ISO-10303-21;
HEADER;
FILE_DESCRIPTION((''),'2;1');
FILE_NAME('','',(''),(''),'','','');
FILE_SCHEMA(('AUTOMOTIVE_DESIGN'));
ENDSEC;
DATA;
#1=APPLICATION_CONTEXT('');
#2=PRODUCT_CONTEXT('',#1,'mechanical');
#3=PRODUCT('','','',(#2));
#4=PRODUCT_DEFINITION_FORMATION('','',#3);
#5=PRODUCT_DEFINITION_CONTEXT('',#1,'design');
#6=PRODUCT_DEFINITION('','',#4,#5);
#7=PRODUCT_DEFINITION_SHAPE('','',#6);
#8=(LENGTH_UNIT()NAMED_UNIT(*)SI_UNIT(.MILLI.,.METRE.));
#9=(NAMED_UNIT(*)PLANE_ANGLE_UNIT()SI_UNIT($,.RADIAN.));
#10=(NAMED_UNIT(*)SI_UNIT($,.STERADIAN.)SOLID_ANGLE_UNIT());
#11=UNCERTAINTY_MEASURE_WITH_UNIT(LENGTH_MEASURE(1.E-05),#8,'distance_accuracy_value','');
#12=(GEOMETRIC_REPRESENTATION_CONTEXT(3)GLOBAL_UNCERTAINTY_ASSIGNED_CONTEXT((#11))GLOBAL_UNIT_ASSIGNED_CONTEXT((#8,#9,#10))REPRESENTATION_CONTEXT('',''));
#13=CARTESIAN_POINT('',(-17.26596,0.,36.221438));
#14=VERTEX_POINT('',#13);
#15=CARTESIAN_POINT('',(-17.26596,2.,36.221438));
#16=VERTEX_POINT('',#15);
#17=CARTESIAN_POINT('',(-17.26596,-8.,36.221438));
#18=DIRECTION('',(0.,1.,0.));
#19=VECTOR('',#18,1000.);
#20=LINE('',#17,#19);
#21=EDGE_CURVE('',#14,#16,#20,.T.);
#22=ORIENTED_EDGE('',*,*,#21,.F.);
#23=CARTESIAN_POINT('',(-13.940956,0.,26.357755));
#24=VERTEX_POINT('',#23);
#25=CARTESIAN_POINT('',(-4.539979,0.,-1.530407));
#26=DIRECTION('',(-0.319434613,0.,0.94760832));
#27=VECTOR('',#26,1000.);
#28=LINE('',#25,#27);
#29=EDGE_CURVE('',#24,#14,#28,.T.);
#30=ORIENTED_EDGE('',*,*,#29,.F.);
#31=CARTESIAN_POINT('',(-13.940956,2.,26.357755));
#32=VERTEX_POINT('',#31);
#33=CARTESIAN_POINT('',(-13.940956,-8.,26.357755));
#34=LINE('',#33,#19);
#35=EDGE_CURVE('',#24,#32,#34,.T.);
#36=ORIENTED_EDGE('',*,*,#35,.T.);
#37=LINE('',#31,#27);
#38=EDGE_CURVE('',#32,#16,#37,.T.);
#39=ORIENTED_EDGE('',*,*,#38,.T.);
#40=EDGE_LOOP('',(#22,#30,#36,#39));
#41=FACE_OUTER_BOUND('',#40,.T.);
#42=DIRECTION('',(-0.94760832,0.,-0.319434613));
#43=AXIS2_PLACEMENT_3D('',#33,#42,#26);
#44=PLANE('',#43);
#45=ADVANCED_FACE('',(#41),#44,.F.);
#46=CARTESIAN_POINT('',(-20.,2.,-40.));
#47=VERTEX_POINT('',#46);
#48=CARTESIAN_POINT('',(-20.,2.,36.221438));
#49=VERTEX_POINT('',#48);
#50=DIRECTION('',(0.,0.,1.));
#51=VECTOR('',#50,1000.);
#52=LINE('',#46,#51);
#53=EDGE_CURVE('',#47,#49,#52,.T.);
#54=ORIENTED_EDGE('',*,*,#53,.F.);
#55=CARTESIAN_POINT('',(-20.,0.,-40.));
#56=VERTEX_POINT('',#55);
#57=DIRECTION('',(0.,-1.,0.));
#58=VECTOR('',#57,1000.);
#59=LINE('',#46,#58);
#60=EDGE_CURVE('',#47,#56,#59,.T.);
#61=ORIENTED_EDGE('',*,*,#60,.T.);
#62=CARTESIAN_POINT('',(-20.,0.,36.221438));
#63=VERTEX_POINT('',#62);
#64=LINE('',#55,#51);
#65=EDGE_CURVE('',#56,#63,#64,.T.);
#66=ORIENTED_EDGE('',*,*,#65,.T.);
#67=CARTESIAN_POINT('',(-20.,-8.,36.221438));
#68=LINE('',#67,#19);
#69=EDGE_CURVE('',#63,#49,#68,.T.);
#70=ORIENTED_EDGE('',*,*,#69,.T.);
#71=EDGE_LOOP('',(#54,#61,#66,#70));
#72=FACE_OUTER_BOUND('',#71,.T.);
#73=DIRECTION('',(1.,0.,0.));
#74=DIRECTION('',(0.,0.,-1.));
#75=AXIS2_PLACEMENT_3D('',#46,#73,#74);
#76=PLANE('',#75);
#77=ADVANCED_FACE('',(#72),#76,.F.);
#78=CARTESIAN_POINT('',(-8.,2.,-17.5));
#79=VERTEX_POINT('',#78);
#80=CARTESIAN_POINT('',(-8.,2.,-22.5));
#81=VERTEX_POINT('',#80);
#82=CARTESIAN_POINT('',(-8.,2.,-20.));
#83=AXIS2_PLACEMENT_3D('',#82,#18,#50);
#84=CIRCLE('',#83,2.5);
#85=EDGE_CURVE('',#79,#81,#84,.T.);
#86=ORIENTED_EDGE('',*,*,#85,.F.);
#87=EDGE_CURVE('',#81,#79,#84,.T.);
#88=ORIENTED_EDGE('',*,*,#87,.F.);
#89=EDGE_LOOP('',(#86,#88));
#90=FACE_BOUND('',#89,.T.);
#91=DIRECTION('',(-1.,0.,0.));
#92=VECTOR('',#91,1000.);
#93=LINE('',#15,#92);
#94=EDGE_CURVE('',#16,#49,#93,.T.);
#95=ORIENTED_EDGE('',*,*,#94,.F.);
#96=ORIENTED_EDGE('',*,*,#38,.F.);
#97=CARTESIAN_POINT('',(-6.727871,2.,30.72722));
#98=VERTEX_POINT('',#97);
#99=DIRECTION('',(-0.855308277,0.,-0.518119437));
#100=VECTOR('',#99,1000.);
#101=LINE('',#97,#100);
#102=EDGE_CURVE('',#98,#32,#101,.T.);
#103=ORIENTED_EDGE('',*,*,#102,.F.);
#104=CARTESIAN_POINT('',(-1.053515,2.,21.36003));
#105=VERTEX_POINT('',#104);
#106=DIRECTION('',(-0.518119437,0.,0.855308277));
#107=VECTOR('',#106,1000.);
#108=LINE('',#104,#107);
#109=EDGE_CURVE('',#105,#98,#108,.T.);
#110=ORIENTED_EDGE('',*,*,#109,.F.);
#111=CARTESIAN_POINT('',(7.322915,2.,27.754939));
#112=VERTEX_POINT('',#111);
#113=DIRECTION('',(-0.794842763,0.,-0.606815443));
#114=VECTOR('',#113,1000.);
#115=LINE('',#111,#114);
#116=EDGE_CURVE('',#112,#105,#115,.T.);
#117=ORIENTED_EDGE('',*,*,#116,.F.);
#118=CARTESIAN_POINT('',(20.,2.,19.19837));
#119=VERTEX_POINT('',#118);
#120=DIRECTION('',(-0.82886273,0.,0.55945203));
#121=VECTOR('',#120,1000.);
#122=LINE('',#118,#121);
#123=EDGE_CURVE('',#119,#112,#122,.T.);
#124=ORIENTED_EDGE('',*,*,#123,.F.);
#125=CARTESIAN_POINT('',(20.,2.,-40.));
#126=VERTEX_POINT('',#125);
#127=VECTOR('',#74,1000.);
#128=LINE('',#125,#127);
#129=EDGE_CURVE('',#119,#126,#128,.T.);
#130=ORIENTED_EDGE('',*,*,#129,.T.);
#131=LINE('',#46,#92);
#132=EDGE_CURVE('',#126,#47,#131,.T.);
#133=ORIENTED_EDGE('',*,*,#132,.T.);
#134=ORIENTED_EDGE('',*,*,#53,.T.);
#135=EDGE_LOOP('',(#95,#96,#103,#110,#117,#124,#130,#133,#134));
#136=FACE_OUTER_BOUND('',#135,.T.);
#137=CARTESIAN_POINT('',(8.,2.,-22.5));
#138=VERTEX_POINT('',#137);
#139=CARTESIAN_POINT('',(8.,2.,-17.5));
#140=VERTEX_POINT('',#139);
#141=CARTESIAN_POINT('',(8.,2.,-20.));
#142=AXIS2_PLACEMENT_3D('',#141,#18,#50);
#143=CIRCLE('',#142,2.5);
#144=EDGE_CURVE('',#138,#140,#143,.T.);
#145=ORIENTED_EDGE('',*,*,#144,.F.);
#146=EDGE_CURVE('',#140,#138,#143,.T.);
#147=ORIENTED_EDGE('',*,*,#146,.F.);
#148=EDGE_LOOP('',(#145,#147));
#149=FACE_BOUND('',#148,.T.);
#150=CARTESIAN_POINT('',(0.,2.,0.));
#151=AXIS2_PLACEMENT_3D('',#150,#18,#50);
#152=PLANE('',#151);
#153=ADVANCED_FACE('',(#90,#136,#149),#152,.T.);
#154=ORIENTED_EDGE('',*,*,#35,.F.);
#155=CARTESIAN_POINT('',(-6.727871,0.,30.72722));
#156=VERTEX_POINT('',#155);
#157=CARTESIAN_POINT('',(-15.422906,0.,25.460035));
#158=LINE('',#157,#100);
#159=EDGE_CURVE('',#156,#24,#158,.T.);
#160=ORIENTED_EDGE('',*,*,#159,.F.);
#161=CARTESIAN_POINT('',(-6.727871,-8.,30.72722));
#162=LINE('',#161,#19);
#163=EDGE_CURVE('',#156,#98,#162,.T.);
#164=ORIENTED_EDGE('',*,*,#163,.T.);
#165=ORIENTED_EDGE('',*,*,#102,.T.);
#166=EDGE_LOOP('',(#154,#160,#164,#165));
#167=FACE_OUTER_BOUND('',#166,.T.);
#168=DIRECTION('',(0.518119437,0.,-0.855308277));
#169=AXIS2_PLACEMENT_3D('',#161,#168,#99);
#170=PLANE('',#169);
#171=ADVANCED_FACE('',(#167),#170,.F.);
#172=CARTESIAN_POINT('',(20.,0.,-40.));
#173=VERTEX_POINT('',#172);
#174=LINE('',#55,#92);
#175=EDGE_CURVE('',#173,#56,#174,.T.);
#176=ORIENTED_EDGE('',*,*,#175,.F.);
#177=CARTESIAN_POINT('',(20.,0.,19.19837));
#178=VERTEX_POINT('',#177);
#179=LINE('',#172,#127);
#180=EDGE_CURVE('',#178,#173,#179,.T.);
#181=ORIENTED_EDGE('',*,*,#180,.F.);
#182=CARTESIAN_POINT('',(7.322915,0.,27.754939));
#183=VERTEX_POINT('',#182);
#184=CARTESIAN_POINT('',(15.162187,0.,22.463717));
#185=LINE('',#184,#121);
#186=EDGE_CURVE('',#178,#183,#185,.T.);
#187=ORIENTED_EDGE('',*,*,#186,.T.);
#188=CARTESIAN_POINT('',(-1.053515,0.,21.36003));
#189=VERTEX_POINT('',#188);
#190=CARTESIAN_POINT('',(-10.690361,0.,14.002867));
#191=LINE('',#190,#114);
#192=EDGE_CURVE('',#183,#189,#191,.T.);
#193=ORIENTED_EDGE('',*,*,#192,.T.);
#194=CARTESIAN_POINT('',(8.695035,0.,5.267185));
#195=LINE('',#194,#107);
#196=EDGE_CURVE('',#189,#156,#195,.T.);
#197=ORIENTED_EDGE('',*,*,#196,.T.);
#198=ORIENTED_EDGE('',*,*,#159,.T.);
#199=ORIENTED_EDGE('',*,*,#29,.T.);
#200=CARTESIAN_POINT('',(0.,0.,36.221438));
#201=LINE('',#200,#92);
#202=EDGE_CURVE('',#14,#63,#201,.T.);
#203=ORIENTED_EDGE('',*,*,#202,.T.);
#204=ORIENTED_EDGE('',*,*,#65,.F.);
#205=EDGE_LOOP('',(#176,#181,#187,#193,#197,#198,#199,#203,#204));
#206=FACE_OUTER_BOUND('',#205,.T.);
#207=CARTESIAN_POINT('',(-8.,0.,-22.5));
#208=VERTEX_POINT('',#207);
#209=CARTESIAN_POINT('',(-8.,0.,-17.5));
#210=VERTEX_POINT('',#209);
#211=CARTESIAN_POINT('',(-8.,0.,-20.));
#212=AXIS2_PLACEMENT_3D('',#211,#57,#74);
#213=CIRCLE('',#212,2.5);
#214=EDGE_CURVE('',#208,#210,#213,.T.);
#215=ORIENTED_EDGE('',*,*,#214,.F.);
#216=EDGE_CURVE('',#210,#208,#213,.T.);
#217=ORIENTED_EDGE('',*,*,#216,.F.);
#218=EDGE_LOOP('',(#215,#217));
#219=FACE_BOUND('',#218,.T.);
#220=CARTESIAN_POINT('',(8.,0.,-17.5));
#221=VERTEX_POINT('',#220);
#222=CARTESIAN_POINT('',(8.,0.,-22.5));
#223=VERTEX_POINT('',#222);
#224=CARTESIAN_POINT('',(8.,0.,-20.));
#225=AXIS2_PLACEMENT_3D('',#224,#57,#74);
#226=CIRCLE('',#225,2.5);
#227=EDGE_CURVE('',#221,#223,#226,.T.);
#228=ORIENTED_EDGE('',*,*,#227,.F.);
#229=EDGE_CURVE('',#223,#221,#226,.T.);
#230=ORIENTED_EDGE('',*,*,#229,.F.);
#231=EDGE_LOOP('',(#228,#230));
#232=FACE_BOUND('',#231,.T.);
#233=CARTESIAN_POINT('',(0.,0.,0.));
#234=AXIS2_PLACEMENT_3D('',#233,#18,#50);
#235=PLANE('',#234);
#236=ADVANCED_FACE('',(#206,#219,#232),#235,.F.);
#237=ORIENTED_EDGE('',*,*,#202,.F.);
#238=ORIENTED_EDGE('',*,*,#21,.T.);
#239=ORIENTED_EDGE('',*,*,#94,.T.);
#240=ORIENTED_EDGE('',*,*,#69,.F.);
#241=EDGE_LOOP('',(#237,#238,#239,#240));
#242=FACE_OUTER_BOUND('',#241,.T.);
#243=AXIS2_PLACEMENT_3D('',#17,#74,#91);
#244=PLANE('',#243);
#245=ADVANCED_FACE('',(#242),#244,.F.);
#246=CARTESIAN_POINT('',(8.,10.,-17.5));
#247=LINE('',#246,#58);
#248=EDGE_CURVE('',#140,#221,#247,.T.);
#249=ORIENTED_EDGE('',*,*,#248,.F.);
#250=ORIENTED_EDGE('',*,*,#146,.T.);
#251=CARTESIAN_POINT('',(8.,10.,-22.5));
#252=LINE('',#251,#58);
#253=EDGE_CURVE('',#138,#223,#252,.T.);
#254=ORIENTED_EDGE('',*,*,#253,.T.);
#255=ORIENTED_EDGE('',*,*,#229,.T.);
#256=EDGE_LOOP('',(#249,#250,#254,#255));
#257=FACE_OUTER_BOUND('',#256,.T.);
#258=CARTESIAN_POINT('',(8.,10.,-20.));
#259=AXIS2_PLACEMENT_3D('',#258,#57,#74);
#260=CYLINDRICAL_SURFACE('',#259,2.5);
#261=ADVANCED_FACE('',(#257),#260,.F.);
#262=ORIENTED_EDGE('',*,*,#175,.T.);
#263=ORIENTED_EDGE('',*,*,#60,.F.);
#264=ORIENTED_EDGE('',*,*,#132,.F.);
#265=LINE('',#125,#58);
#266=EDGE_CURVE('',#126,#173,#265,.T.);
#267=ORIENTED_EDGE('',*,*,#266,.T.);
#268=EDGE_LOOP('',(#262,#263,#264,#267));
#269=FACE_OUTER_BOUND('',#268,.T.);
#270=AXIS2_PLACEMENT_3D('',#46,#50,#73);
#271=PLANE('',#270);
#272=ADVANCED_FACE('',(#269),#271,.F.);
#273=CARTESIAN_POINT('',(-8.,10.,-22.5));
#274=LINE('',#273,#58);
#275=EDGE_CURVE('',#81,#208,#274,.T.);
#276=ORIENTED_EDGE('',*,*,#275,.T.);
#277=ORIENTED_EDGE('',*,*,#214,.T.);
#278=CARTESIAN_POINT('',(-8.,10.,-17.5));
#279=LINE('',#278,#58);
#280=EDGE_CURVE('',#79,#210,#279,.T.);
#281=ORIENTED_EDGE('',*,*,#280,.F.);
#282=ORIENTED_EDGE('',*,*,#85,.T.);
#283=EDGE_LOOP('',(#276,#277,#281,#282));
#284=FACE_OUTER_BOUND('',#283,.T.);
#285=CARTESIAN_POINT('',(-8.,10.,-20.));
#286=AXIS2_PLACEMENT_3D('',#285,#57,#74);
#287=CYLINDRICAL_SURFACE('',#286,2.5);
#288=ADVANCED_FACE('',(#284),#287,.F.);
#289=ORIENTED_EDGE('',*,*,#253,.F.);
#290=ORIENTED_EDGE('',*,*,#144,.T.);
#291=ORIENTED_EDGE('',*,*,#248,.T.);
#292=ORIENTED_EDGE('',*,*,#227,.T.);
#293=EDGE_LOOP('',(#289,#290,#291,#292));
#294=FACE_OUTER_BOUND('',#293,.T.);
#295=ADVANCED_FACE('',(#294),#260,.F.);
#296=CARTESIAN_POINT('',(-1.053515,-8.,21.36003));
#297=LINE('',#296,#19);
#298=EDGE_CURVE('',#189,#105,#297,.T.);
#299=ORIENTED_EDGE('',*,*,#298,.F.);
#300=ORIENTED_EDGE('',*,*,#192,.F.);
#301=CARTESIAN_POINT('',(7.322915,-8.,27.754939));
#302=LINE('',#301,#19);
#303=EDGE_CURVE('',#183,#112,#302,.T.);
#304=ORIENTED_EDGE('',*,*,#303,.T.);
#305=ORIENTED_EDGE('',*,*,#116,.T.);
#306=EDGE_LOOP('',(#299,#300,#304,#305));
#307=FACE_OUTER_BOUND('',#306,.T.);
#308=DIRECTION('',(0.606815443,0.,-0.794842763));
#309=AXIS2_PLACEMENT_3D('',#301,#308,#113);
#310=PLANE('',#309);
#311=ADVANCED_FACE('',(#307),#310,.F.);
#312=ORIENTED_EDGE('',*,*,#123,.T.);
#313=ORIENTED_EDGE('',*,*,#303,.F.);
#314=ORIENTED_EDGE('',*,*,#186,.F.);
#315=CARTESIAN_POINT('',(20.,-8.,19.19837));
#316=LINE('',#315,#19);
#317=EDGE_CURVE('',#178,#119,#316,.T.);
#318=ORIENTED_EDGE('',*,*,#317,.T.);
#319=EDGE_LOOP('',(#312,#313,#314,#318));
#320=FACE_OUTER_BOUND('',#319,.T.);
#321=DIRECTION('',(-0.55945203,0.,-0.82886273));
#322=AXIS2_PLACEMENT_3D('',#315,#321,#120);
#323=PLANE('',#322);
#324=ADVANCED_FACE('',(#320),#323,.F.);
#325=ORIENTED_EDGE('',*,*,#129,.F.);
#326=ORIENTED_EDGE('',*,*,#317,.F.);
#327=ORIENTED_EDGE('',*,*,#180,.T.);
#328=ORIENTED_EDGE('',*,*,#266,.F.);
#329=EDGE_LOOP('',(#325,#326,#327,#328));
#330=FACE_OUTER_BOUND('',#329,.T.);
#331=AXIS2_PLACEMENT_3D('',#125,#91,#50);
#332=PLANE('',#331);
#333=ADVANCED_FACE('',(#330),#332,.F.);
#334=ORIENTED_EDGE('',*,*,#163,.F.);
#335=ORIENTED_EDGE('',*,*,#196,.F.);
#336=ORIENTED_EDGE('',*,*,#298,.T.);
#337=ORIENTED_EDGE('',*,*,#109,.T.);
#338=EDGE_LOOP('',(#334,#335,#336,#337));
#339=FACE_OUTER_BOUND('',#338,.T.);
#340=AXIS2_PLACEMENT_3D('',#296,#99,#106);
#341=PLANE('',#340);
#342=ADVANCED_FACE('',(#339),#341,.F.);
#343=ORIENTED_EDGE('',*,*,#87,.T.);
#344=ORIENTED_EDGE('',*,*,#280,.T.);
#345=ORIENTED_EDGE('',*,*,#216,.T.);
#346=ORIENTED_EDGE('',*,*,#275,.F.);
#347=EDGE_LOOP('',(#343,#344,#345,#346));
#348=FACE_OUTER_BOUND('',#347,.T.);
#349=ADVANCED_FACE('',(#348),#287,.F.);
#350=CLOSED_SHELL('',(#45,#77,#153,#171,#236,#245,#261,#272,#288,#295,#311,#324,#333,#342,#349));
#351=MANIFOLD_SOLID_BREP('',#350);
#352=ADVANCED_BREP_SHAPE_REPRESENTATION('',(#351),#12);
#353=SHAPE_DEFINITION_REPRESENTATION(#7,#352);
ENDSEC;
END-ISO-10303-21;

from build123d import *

# Parameters (mm, degrees)
SKETCH1_W           = 40
SKETCH1_H           = 80
BOSS_EXTRUDE1_DEPTH = 2
SKETCH2_R           = 2.5
CUT_EXTRUDE1_DEPTH  = 10
CUT_EXTRUDE2_DEPTH  = 10


with BuildPart() as part:
    # Sketch1 → Boss-Extrude1 (new body)
    with BuildSketch(Plane(origin=(0, 0, 0), x_dir=(1, 0, 0), z_dir=(0, 1, 0))):
        Rectangle(SKETCH1_W, SKETCH1_H)
    extrude(amount=BOSS_EXTRUDE1_DEPTH)

    # Sketch2 → Cut-Extrude1 (cut)
    with BuildSketch(Plane.XZ):
        with Locations(Location((8, -20, 0), (0, 0, 270))):
            Circle(SKETCH2_R)
        with Locations(Location((-8, -20, 0), (0, 0, 270))):
            Circle(SKETCH2_R)
    extrude(amount=-CUT_EXTRUDE1_DEPTH, mode=Mode.SUBTRACT)

    # Sketch3 → Cut-Extrude2 (cut)
    with BuildSketch(Plane(origin=(0, 2, 0), x_dir=(1, 0, 0), z_dir=(0, 1, 0))):
        Polygon((20, -19.19837027), (7.322915473, -27.754938711), (-1.053514684, -21.360029666), (-6.727870598, -30.72722038), (-13.940955905, -26.357755241), (-17.265960151, -36.22143801), (-20, -36.22143801), (-20, -40), (20, -40), align=None)
    extrude(amount=-CUT_EXTRUDE2_DEPTH, mode=Mode.SUBTRACT)


solid = part.part
